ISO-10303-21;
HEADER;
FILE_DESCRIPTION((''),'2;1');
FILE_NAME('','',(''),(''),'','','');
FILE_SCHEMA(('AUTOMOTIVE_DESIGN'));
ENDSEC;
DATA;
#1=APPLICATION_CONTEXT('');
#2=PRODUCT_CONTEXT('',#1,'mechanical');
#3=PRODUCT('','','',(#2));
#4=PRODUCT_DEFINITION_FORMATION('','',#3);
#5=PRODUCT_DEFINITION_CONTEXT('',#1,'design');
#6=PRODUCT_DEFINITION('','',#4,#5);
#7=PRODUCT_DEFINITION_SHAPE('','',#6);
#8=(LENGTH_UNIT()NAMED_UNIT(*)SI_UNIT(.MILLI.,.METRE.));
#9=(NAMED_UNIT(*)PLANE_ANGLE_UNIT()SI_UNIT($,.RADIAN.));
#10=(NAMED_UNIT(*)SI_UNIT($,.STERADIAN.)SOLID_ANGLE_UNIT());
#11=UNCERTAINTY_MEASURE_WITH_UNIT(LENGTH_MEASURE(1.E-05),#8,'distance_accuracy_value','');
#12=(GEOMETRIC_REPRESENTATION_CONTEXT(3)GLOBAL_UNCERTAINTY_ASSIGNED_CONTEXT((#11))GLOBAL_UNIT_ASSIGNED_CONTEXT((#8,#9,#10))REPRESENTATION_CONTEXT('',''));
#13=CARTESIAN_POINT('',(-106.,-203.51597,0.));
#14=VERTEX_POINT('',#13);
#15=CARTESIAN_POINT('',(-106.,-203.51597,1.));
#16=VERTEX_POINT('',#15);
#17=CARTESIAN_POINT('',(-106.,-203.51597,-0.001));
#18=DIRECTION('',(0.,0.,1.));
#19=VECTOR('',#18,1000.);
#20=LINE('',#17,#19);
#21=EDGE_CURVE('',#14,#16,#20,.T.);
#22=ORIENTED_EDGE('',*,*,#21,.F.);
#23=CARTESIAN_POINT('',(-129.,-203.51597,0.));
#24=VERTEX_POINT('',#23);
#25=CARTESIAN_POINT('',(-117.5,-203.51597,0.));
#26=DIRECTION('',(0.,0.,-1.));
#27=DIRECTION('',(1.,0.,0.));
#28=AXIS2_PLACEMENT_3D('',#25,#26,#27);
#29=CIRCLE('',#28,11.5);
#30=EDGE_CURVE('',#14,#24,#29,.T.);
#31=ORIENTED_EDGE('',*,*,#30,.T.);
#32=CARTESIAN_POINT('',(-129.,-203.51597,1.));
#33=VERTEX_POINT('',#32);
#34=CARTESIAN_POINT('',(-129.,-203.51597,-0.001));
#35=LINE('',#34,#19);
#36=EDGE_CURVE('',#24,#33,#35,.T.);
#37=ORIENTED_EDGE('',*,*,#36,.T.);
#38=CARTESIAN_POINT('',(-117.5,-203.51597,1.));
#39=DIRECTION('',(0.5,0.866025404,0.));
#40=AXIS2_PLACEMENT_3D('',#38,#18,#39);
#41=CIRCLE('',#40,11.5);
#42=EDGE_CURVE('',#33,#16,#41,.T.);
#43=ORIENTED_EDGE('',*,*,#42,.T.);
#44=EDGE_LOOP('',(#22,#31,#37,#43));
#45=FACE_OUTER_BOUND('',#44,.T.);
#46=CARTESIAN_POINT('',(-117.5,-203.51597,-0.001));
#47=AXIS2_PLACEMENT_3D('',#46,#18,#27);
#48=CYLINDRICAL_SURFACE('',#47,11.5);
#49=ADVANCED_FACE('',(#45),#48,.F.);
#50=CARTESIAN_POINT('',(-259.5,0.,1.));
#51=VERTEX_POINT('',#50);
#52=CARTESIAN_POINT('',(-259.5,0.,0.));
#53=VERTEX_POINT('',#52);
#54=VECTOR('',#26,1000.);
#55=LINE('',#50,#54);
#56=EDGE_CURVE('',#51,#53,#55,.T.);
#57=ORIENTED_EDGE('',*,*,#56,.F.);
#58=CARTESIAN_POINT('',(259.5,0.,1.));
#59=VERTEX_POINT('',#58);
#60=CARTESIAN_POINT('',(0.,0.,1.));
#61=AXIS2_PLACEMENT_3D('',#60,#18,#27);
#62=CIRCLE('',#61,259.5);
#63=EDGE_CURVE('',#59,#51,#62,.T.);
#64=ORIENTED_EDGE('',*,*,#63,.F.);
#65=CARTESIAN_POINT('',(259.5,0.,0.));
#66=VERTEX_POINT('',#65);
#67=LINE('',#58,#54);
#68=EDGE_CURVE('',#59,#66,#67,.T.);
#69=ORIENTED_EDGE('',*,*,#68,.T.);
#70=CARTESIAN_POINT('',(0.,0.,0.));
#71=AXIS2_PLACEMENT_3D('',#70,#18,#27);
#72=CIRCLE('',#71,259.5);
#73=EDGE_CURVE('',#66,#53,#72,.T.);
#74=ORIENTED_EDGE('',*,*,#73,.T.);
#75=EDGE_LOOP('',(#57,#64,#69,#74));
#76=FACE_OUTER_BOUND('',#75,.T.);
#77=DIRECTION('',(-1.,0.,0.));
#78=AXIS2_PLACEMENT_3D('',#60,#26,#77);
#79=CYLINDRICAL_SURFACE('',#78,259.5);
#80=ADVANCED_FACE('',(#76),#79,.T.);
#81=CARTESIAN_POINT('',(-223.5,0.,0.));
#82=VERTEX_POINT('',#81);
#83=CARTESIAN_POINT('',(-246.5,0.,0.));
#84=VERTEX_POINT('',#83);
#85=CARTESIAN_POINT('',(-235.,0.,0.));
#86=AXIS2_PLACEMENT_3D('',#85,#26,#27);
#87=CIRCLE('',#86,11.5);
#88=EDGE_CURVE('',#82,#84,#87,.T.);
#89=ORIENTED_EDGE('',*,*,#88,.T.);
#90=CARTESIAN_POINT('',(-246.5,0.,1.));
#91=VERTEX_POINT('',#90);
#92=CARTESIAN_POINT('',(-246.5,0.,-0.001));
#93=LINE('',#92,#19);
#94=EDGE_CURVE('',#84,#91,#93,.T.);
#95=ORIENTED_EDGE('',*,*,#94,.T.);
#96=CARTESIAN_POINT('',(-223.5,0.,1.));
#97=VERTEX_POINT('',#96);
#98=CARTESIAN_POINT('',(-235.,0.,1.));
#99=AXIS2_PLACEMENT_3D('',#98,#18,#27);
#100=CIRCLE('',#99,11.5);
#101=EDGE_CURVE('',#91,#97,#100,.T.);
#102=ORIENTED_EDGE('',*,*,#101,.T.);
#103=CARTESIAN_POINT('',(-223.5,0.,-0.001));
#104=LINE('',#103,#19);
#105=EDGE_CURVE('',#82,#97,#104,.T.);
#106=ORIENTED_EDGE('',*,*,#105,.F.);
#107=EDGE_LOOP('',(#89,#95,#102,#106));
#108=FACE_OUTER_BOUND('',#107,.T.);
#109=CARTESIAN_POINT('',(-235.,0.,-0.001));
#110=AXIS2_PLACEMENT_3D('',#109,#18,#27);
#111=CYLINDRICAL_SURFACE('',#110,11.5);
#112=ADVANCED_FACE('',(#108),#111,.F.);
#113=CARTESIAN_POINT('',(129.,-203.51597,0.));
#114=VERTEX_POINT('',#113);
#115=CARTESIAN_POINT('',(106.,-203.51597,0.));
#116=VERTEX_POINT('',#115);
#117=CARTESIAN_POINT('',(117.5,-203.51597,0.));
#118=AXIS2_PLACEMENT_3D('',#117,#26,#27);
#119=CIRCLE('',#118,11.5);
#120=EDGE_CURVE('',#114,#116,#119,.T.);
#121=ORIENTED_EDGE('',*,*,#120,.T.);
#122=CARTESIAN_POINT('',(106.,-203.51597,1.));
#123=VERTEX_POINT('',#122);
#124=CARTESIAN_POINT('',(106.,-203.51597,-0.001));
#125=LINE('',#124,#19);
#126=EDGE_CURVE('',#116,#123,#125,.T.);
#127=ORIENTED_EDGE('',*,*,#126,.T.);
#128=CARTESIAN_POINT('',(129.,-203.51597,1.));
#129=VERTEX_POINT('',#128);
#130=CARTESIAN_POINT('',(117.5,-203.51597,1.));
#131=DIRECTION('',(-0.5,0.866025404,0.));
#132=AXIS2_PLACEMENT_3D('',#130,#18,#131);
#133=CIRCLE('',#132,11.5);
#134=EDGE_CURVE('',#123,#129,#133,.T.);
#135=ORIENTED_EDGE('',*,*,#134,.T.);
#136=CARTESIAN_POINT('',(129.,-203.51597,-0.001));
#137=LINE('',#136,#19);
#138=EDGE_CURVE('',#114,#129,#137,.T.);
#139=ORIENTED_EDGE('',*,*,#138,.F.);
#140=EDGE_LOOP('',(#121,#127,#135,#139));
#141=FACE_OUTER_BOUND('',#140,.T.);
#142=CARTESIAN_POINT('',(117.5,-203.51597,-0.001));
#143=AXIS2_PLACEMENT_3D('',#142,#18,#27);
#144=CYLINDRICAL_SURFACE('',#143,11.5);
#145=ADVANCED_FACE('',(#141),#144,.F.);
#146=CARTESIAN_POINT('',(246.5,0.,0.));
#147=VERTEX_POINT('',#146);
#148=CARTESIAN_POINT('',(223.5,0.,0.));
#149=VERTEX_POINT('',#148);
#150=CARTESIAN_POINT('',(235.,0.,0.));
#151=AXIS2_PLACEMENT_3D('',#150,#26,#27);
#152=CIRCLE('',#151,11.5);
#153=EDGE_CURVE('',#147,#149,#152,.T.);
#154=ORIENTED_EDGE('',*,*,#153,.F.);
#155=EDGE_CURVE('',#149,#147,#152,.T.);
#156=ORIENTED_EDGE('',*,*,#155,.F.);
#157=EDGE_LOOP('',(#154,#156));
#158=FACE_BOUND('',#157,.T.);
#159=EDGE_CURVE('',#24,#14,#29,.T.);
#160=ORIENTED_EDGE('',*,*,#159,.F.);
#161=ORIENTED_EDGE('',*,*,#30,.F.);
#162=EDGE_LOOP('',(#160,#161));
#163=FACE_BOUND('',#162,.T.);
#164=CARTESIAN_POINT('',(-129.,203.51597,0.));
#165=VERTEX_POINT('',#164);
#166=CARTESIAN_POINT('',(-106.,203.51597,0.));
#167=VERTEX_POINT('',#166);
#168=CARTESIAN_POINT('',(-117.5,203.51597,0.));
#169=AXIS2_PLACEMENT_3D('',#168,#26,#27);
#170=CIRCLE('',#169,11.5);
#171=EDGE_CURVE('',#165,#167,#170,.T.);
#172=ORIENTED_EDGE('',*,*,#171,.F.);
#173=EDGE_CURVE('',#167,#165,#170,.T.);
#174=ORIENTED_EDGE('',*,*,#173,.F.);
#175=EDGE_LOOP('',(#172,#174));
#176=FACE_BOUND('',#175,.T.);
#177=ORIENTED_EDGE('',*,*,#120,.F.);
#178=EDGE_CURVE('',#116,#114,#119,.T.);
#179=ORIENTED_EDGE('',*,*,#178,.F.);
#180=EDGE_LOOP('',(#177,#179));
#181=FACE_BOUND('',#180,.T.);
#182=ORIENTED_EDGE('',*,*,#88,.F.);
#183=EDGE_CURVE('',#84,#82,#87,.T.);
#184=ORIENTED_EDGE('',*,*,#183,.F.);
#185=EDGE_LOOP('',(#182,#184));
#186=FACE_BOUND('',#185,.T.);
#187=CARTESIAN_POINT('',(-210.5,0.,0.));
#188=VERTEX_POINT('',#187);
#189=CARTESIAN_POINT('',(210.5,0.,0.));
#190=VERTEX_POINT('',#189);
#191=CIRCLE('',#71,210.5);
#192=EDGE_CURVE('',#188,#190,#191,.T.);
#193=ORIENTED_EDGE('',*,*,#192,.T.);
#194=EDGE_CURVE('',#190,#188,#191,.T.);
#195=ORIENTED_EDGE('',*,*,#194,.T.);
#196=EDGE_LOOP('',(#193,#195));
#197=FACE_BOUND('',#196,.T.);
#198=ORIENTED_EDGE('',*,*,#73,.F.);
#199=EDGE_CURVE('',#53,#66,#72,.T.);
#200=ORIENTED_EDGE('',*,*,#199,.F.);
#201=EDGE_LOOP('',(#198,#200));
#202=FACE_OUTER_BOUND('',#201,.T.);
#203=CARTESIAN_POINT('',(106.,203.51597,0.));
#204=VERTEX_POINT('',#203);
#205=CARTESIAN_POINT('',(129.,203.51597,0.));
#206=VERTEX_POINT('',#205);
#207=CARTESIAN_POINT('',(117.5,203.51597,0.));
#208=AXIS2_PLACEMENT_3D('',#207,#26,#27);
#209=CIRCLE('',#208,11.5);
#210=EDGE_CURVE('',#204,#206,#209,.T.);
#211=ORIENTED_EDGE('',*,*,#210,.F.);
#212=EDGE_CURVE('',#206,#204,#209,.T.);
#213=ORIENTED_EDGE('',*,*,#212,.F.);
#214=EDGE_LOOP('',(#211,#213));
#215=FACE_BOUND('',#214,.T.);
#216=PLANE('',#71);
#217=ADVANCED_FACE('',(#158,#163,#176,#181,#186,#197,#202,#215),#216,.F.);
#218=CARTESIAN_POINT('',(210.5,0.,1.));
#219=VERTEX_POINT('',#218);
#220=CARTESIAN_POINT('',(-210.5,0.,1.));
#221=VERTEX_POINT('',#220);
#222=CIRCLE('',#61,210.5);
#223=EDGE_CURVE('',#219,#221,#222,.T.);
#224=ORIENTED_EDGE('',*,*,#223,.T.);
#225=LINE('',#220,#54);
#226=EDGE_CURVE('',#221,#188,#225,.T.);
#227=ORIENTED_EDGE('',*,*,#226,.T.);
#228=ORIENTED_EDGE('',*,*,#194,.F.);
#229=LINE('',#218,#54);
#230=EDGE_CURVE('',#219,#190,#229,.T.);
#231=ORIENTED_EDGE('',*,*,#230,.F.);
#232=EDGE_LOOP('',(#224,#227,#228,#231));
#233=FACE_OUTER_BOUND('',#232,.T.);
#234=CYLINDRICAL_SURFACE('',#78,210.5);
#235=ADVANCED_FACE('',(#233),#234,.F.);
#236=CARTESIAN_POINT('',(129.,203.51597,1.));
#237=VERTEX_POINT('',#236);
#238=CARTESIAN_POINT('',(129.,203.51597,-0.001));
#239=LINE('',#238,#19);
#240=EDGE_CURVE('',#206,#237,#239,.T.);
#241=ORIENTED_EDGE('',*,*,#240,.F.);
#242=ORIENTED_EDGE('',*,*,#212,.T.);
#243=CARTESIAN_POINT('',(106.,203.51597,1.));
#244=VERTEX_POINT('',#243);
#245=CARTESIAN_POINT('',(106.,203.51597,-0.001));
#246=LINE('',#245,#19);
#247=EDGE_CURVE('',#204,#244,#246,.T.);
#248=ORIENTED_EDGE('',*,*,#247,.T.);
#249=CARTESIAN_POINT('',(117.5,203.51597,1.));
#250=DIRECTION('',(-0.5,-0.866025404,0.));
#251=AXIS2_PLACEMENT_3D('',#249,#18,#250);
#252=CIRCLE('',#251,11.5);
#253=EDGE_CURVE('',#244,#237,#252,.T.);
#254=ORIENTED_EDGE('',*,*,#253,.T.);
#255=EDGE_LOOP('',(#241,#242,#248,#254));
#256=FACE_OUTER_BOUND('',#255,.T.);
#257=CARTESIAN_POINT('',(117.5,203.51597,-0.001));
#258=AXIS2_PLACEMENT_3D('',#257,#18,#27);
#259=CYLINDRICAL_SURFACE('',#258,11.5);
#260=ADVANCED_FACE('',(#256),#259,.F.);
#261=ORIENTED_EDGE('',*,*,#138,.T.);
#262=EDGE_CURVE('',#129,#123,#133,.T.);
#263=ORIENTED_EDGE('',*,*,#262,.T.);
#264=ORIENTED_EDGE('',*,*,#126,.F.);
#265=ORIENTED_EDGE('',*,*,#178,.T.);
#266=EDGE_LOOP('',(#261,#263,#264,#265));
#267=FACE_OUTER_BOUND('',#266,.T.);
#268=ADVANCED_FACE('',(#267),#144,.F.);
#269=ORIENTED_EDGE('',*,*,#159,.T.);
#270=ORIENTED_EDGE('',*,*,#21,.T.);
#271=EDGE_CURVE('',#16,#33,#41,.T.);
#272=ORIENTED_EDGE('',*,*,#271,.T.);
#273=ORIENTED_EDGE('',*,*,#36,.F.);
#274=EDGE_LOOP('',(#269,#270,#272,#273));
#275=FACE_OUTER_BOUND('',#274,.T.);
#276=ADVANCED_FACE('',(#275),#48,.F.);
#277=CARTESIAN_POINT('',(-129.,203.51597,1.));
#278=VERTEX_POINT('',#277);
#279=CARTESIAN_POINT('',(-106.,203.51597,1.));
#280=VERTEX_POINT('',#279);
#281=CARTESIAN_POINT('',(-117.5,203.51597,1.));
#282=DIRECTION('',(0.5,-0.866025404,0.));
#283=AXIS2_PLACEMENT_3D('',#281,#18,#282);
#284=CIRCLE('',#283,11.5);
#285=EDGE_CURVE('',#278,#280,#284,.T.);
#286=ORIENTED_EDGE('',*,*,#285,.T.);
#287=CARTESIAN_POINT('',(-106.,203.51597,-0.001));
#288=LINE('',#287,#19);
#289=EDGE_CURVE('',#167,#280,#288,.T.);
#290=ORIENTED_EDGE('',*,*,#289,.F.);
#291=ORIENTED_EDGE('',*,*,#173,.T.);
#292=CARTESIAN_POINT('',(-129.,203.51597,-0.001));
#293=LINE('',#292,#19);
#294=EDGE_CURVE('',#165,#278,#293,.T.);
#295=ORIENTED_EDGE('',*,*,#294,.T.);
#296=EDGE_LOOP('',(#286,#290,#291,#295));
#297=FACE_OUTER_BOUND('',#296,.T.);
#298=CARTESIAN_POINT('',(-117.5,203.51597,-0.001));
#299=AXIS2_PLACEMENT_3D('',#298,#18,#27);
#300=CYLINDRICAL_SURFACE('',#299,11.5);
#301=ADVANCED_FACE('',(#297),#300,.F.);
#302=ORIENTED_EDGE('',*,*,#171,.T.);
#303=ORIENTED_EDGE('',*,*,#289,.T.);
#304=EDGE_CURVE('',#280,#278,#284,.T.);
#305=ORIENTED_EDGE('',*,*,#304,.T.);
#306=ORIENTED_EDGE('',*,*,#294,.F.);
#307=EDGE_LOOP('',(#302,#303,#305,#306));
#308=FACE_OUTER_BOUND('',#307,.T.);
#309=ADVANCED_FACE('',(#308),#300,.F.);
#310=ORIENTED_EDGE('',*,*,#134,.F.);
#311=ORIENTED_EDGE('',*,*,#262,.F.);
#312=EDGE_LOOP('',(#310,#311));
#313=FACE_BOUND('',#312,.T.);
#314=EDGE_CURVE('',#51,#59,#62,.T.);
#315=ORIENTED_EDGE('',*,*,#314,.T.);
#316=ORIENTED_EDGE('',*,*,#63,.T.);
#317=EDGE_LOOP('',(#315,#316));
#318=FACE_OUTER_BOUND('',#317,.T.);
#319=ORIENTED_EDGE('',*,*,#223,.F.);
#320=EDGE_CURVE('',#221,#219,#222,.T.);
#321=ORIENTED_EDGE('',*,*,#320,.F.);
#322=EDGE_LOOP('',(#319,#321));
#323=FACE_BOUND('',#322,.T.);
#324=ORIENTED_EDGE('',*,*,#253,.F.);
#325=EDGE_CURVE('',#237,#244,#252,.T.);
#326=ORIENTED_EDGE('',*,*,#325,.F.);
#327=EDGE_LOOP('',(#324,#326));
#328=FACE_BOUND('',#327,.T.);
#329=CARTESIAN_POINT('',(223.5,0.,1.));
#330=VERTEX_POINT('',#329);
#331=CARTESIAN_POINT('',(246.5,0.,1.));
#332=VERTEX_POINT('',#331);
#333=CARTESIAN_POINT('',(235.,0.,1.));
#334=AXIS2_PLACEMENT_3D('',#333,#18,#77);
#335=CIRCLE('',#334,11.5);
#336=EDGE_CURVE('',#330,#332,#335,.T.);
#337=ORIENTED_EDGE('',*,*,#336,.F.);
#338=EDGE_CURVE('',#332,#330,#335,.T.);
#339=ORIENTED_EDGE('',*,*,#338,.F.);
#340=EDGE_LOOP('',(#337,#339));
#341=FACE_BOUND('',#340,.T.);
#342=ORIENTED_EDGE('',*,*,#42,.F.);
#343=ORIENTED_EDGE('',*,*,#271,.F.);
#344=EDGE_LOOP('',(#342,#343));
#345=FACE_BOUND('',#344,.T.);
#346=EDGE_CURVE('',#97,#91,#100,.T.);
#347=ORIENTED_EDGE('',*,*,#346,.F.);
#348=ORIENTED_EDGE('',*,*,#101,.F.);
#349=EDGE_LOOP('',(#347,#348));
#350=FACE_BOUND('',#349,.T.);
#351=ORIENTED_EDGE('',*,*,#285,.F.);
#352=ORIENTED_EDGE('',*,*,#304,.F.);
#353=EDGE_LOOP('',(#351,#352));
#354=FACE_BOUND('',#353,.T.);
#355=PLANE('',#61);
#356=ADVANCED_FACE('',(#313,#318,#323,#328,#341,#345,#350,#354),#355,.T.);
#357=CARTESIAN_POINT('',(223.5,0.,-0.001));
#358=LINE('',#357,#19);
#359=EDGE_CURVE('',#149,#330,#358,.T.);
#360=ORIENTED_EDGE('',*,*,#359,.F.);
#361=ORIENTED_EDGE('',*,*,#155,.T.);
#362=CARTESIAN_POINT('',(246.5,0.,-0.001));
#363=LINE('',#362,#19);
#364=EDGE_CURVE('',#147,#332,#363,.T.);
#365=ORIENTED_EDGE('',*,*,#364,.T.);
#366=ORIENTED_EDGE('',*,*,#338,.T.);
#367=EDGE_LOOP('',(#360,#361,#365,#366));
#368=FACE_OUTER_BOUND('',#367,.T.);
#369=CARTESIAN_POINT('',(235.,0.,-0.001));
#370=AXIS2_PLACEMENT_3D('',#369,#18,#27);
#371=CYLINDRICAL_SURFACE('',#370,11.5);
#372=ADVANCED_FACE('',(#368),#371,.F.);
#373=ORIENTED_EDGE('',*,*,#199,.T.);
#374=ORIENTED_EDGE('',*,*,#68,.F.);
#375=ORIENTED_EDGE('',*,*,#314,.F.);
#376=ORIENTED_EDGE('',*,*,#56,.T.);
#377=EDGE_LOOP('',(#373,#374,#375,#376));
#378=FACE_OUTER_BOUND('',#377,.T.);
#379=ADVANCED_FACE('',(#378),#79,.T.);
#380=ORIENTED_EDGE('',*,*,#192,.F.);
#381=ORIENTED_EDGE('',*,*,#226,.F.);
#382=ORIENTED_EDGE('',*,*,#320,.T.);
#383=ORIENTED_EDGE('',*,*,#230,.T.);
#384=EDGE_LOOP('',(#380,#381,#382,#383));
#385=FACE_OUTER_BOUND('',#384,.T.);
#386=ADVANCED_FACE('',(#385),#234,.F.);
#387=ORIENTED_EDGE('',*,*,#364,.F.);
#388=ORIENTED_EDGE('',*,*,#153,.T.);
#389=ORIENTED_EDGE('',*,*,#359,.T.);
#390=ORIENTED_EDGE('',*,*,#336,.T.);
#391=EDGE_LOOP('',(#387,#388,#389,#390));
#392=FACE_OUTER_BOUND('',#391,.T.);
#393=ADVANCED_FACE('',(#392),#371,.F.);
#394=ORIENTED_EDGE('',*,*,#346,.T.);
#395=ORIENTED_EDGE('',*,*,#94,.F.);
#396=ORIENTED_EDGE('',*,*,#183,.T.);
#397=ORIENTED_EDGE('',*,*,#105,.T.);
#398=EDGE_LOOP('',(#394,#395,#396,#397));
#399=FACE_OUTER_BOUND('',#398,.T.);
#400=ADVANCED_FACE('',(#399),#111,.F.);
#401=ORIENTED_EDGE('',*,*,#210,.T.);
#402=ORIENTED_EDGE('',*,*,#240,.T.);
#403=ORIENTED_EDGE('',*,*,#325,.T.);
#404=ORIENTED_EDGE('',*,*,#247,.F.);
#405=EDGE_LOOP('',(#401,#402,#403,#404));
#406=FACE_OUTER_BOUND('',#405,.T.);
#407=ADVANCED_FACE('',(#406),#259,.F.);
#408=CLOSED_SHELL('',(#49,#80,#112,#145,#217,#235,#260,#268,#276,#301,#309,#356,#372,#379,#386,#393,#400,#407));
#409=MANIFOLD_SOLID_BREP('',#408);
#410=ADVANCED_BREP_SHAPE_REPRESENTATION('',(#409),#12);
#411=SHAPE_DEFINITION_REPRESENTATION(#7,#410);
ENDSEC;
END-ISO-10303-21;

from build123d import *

# Parameters (mm, degrees)
SKETCH1_R           = 259.5
SKETCH1_R_2         = 210.5
BOSS_EXTRUDE1_DEPTH = 1
CUT_EXTRUDE1_REACH  = 368.99
SKETCH2_R           = 11.5
CIRPATTERN1_COUNT   = 6


with BuildPart() as part:
    # Sketch1 → Boss-Extrude1 (new body)
    with BuildSketch(Plane.XY):
        Circle(SKETCH1_R)
        Circle(SKETCH1_R_2, mode=Mode.SUBTRACT)
    extrude(amount=BOSS_EXTRUDE1_DEPTH)

    # Sketch2 → Cut-Extrude1 (cut, up to next)
    with BuildSketch(Plane.XY.offset(1), mode=Mode.PRIVATE) as cut_extrude1_sk1:
        with Locations((-235, 0)):
            Circle(SKETCH2_R)
    cut_extrude1_tool1 = extrude(cut_extrude1_sk1.sketch, amount=-CUT_EXTRUDE1_REACH, mode=Mode.PRIVATE) & part.part
    cut_extrude1 = cut_extrude1_tool1.solids().sort_by_distance((-235, 0, 1))[0]
    add(cut_extrude1, mode=Mode.SUBTRACT)

    # CirPattern1: Cut-Extrude1 ×6 about axis
    cirpattern1_axis = Axis((0, 0, 0), (0, 0, 1))
    for i in range(1, CIRPATTERN1_COUNT):
        add(cut_extrude1.rotate(cirpattern1_axis, i * 360 / CIRPATTERN1_COUNT), mode=Mode.SUBTRACT)


solid = part.part
